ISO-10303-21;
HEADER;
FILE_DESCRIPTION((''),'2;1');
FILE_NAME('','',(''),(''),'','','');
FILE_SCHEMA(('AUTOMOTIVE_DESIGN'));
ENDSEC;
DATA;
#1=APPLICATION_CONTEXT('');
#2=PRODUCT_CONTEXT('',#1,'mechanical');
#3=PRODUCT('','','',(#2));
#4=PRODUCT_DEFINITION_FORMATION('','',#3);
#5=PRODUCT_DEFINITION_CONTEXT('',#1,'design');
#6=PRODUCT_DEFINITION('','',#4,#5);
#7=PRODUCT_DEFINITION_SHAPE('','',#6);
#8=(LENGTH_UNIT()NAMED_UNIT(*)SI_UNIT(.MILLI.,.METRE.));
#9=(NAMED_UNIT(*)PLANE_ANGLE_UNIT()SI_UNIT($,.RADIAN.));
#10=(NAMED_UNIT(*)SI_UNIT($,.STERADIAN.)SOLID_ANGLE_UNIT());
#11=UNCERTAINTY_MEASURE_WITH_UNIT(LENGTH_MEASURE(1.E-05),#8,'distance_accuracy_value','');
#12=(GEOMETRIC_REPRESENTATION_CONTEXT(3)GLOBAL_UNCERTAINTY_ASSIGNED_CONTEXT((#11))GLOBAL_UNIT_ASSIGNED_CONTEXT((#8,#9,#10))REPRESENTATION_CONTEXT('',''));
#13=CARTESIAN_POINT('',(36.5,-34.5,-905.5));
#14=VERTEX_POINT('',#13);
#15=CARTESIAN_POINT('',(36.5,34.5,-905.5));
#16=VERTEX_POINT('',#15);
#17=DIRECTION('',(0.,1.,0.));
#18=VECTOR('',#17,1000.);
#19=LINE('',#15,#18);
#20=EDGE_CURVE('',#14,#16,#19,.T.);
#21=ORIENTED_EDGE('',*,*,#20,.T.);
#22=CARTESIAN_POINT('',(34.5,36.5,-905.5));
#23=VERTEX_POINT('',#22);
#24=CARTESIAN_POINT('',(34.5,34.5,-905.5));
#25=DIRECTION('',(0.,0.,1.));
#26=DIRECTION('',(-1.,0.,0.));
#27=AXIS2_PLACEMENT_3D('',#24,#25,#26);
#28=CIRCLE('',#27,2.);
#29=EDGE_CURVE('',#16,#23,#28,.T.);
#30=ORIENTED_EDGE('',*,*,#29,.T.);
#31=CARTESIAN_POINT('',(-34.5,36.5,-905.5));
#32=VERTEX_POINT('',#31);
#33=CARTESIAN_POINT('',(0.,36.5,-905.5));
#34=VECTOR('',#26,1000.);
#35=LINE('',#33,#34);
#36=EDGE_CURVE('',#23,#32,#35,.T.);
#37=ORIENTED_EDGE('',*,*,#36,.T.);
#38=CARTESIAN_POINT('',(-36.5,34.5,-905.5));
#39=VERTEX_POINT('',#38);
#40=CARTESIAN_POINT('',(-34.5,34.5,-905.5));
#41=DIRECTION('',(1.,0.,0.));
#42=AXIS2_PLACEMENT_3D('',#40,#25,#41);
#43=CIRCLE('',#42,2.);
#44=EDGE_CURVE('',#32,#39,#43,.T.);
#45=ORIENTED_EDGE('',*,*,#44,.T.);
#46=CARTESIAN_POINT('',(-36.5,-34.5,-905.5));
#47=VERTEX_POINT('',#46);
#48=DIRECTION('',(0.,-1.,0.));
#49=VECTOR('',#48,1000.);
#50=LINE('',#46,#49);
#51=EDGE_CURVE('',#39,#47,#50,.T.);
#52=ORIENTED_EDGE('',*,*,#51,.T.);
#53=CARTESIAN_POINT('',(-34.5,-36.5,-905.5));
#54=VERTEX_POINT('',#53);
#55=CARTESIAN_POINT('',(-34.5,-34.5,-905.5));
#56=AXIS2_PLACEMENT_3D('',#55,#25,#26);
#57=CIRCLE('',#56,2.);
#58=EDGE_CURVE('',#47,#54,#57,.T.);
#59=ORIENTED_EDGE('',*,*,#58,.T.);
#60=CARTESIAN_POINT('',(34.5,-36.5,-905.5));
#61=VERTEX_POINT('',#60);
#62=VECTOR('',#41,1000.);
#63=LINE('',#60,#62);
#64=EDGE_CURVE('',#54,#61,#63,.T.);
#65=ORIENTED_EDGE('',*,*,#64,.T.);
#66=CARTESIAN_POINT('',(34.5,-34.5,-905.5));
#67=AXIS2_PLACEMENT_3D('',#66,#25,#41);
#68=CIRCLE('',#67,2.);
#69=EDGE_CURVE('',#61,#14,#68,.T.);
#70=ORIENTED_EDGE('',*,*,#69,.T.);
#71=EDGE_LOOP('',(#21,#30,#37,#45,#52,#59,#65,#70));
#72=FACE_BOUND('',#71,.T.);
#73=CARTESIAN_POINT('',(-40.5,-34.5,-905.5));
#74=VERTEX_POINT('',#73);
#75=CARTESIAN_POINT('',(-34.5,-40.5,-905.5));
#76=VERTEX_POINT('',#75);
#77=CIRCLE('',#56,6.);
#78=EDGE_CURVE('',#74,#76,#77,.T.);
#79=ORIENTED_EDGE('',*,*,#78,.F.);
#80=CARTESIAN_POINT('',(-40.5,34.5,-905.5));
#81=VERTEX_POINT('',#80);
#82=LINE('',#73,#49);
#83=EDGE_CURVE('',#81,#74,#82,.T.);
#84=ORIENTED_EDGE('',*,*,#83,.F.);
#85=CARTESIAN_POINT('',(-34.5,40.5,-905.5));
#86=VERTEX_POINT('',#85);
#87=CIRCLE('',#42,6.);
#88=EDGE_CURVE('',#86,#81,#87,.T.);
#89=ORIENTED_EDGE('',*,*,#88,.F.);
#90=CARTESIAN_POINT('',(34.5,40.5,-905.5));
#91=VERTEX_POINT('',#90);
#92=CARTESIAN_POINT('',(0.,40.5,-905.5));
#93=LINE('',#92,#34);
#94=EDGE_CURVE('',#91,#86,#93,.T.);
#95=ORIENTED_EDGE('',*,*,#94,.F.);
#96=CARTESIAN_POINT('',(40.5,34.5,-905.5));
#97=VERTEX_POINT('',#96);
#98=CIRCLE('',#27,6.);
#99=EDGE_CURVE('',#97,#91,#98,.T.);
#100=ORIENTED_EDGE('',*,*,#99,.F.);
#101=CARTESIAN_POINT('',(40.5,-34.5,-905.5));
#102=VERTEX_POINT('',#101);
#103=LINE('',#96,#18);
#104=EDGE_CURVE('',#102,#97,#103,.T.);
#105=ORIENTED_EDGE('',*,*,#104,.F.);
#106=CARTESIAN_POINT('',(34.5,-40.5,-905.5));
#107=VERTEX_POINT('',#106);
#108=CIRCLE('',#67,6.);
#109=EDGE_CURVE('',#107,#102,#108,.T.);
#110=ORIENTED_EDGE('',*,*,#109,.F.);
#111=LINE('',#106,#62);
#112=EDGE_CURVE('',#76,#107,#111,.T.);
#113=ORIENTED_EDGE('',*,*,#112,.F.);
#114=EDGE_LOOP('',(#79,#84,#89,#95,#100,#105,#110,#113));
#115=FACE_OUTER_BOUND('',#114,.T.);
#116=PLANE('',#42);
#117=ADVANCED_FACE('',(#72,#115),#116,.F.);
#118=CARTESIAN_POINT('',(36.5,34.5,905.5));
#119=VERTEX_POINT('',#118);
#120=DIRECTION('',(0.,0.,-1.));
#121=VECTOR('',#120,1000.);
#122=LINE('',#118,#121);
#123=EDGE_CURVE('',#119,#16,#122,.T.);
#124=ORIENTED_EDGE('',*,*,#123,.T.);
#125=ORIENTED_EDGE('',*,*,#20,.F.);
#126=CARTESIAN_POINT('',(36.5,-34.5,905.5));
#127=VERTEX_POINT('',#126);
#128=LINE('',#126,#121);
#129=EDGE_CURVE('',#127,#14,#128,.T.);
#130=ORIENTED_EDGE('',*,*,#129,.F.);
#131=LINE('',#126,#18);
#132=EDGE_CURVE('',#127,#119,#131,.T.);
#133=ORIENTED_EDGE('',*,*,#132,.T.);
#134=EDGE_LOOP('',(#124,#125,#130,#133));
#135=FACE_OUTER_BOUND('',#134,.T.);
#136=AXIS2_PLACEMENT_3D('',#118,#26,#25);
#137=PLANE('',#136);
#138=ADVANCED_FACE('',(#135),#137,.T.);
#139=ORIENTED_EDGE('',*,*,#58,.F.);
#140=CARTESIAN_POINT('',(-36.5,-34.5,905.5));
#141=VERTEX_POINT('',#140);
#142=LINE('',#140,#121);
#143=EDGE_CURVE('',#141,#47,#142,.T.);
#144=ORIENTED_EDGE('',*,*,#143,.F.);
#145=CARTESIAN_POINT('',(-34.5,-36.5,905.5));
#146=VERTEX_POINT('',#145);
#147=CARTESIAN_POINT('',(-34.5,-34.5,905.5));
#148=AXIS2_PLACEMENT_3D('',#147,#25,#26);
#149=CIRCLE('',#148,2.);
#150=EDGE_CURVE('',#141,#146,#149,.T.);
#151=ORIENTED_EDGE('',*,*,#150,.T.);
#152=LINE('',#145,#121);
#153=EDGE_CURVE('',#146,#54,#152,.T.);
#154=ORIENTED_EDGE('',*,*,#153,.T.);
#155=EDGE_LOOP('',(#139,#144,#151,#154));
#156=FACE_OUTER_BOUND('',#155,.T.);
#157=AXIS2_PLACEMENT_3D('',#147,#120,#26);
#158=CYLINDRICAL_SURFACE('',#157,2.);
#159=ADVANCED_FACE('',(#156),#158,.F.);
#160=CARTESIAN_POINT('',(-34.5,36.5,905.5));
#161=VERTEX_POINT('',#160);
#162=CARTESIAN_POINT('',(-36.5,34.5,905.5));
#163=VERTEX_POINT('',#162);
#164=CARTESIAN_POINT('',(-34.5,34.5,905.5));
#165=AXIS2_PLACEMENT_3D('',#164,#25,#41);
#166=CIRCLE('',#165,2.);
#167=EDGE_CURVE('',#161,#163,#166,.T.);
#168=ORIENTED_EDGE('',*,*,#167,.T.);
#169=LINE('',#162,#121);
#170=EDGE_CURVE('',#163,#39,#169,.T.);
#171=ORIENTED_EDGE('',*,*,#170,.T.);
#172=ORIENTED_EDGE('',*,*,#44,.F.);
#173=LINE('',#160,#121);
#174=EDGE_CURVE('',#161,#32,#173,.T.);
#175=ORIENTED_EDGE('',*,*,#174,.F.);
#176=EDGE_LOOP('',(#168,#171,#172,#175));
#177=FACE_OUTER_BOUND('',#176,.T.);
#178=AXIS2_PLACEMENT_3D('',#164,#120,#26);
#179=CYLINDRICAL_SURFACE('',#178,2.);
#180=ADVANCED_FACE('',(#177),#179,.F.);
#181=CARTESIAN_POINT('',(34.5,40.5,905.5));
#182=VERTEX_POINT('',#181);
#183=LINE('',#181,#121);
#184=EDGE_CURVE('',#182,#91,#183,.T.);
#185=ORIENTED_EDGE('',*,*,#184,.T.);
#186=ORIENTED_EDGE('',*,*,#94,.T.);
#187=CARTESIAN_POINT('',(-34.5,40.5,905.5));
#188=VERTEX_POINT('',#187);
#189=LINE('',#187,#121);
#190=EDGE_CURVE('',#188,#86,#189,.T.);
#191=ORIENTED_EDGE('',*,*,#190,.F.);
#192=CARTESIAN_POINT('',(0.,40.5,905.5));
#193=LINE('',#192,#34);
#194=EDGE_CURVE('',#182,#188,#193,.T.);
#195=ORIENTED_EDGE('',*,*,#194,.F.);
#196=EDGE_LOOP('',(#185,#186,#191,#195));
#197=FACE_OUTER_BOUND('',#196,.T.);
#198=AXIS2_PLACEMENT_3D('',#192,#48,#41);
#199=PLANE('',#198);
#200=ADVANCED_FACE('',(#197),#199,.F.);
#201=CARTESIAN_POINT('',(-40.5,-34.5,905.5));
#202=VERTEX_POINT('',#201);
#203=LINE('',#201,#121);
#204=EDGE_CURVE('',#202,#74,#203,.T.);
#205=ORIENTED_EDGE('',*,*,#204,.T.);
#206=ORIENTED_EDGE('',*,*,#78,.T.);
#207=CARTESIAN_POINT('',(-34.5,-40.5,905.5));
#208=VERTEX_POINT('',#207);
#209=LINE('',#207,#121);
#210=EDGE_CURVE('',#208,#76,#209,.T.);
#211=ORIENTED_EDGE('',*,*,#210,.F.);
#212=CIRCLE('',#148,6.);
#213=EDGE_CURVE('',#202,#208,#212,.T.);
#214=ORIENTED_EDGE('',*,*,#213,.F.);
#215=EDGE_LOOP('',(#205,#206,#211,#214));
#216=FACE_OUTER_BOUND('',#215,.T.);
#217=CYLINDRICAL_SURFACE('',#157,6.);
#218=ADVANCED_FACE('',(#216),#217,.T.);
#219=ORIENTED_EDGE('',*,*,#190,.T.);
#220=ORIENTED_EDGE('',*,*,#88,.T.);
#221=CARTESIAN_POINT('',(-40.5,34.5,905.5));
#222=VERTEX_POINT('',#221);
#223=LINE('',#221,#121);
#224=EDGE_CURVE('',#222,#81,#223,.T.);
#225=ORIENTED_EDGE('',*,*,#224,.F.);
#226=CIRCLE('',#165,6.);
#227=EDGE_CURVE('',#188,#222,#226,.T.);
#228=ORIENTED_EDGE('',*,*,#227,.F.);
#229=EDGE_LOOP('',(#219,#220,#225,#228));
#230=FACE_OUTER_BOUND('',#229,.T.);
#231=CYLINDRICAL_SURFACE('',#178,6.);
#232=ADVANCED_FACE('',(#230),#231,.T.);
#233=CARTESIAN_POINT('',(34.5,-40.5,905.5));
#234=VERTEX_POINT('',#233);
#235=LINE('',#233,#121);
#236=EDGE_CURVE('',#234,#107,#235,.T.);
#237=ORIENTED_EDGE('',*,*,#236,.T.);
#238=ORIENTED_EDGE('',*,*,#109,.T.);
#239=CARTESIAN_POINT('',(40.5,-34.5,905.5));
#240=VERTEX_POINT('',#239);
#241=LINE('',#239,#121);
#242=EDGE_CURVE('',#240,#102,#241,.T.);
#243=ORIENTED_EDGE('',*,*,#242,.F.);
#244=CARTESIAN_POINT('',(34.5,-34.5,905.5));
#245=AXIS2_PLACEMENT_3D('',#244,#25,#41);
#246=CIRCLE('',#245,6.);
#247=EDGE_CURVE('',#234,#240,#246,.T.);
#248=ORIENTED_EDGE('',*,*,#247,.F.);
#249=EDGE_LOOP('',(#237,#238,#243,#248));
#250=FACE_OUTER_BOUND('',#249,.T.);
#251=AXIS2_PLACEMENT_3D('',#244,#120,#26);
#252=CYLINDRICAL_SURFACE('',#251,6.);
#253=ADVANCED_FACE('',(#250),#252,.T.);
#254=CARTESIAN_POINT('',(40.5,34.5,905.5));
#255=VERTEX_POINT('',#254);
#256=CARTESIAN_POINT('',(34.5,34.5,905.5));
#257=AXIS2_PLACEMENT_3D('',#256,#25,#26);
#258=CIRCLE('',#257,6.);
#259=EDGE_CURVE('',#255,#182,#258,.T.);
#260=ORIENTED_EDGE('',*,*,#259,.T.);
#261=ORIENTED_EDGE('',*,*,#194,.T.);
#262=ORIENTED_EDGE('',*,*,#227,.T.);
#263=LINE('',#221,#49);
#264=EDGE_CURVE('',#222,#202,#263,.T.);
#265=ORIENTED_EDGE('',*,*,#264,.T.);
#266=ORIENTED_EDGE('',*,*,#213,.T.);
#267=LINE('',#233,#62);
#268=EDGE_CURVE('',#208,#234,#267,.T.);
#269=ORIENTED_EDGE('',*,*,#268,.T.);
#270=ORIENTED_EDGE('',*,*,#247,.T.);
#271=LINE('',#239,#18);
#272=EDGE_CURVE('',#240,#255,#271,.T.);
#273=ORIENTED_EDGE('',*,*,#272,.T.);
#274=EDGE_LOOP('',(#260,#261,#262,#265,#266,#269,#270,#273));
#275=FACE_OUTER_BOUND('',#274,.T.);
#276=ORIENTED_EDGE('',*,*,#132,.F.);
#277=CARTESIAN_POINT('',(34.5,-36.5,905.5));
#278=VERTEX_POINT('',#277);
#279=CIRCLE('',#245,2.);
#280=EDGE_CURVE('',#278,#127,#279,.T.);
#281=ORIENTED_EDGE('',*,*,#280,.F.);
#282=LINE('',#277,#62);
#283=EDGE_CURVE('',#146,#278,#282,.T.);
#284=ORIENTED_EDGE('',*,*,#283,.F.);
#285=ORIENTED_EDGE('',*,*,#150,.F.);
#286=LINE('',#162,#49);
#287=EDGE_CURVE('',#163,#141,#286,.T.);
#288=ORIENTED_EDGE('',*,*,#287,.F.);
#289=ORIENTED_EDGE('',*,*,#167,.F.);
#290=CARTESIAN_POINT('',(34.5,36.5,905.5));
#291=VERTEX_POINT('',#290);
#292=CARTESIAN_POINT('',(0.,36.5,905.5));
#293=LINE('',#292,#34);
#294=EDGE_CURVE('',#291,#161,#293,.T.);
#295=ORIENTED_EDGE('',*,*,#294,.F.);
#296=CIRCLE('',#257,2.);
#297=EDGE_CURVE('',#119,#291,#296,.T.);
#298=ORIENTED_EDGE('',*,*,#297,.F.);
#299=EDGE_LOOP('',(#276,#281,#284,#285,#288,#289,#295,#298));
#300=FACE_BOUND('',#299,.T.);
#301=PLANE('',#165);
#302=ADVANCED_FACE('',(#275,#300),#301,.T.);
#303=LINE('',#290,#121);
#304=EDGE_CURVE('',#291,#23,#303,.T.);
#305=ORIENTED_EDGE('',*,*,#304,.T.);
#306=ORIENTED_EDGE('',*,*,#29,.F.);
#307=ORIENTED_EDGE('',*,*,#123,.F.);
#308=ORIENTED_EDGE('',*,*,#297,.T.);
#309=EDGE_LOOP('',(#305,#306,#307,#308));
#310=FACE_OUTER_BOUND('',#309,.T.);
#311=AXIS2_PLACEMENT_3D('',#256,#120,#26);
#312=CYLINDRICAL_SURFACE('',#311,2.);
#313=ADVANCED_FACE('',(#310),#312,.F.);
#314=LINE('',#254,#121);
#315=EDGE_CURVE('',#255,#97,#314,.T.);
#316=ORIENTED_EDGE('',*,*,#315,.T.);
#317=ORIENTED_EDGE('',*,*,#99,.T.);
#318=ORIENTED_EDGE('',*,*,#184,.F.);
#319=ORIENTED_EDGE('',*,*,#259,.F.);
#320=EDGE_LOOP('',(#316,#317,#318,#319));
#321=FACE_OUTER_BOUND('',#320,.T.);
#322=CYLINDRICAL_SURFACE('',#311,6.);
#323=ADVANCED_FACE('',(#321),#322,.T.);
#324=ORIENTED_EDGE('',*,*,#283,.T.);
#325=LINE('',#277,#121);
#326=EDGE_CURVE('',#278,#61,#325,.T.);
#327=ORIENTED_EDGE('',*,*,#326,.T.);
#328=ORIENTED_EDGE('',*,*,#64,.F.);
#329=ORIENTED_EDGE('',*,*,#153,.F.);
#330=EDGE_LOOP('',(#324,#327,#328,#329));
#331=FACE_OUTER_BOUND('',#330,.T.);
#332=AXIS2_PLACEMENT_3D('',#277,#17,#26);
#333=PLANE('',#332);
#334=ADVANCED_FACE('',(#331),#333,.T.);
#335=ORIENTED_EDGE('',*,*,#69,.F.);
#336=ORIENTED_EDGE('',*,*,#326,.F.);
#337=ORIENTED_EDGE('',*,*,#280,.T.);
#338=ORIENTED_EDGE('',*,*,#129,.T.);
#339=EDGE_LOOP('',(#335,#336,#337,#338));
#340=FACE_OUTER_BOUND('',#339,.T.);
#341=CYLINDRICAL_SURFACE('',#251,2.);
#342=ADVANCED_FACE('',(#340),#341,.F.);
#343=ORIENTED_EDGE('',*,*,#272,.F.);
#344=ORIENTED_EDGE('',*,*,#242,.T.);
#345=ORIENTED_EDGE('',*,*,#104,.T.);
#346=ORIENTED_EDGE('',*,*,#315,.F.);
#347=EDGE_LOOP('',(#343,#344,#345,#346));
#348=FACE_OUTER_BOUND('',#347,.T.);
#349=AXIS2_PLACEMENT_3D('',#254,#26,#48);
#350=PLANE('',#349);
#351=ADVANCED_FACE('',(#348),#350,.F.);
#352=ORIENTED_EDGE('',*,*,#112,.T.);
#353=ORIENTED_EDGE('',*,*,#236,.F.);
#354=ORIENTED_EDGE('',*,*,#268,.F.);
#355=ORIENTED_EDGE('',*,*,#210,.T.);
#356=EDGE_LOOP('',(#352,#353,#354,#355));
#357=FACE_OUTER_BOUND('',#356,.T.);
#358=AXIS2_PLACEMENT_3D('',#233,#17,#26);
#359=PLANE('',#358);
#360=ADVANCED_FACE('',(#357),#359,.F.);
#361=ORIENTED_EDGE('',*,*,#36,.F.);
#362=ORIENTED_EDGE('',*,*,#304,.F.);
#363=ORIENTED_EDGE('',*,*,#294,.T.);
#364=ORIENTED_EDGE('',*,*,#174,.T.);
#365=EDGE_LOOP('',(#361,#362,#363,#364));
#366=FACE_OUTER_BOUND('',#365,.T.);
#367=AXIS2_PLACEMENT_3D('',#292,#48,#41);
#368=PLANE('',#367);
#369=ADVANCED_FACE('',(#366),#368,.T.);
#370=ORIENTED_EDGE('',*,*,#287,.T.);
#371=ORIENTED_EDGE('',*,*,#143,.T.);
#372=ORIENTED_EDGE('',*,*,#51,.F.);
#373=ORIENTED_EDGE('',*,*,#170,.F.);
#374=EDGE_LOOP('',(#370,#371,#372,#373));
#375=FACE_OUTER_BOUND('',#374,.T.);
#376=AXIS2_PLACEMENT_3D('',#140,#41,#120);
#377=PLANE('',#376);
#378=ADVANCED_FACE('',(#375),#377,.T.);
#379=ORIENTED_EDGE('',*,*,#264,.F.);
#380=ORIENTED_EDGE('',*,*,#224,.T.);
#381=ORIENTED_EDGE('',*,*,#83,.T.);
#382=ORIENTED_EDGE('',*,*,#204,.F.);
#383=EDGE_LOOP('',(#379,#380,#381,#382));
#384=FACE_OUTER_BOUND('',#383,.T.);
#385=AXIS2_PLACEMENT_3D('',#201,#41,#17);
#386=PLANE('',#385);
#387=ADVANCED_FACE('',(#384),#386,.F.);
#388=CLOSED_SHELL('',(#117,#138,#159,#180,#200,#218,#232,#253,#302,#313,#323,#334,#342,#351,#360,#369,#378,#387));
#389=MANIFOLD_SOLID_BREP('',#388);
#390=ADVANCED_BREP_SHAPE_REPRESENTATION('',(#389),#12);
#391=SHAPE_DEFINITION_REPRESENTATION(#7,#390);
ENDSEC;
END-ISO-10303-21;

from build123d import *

# Parameters (mm, degrees)
BOSS_EXTRUDE_1_DEPTH = 905.5


with BuildPart() as part:
    # Sketch 1 → Boss-Extrude 1 (new, symmetric)
    with BuildSketch(Plane.XY):
        with BuildLine():
            Line((0, 40.5), (-34.5, 40.5))
            ThreePointArc((-34.5, 40.5), (-38.742640687, 38.742640687), (-40.5, 34.5))
            Line((-40.5, 34.5), (-40.5, 0))
            Line((-40.5, 0), (-40.5, -34.5))
            ThreePointArc((-40.5, -34.5), (-38.742640687, -38.742640687), (-34.5, -40.5))
            Line((-34.5, -40.5), (34.5, -40.5))
            ThreePointArc((34.5, -40.5), (38.742640687, -38.742640687), (40.5, -34.5))
            Line((40.5, -34.5), (40.5, 0))
            Line((40.5, 0), (40.5, 34.5))
            ThreePointArc((40.5, 34.5), (38.742640687, 38.742640687), (34.5, 40.5))
            Line((34.5, 40.5), (0, 40.5))
        make_face()
        with BuildLine():
            Line((0, 36.5), (-34.5, 36.5))
            ThreePointArc((-34.5, 36.5), (-35.914213562, 35.914213562), (-36.5, 34.5))
            Line((-36.5, 34.5), (-36.5, 0))
            Line((-36.5, 0), (-36.5, -34.5))
            ThreePointArc((-36.5, -34.5), (-35.914213562, -35.914213562), (-34.5, -36.5))
            Line((-34.5, -36.5), (34.5, -36.5))
            ThreePointArc((34.5, -36.5), (35.914213562, -35.914213562), (36.5, -34.5))
            Line((36.5, -34.5), (36.5, 0))
            Line((36.5, 0), (36.5, 34.5))
            ThreePointArc((36.5, 34.5), (35.914213562, 35.914213562), (34.5, 36.5))
            Line((34.5, 36.5), (0, 36.5))
        make_face(mode=Mode.SUBTRACT)
    extrude(amount=BOSS_EXTRUDE_1_DEPTH, both=True)


solid = part.part
